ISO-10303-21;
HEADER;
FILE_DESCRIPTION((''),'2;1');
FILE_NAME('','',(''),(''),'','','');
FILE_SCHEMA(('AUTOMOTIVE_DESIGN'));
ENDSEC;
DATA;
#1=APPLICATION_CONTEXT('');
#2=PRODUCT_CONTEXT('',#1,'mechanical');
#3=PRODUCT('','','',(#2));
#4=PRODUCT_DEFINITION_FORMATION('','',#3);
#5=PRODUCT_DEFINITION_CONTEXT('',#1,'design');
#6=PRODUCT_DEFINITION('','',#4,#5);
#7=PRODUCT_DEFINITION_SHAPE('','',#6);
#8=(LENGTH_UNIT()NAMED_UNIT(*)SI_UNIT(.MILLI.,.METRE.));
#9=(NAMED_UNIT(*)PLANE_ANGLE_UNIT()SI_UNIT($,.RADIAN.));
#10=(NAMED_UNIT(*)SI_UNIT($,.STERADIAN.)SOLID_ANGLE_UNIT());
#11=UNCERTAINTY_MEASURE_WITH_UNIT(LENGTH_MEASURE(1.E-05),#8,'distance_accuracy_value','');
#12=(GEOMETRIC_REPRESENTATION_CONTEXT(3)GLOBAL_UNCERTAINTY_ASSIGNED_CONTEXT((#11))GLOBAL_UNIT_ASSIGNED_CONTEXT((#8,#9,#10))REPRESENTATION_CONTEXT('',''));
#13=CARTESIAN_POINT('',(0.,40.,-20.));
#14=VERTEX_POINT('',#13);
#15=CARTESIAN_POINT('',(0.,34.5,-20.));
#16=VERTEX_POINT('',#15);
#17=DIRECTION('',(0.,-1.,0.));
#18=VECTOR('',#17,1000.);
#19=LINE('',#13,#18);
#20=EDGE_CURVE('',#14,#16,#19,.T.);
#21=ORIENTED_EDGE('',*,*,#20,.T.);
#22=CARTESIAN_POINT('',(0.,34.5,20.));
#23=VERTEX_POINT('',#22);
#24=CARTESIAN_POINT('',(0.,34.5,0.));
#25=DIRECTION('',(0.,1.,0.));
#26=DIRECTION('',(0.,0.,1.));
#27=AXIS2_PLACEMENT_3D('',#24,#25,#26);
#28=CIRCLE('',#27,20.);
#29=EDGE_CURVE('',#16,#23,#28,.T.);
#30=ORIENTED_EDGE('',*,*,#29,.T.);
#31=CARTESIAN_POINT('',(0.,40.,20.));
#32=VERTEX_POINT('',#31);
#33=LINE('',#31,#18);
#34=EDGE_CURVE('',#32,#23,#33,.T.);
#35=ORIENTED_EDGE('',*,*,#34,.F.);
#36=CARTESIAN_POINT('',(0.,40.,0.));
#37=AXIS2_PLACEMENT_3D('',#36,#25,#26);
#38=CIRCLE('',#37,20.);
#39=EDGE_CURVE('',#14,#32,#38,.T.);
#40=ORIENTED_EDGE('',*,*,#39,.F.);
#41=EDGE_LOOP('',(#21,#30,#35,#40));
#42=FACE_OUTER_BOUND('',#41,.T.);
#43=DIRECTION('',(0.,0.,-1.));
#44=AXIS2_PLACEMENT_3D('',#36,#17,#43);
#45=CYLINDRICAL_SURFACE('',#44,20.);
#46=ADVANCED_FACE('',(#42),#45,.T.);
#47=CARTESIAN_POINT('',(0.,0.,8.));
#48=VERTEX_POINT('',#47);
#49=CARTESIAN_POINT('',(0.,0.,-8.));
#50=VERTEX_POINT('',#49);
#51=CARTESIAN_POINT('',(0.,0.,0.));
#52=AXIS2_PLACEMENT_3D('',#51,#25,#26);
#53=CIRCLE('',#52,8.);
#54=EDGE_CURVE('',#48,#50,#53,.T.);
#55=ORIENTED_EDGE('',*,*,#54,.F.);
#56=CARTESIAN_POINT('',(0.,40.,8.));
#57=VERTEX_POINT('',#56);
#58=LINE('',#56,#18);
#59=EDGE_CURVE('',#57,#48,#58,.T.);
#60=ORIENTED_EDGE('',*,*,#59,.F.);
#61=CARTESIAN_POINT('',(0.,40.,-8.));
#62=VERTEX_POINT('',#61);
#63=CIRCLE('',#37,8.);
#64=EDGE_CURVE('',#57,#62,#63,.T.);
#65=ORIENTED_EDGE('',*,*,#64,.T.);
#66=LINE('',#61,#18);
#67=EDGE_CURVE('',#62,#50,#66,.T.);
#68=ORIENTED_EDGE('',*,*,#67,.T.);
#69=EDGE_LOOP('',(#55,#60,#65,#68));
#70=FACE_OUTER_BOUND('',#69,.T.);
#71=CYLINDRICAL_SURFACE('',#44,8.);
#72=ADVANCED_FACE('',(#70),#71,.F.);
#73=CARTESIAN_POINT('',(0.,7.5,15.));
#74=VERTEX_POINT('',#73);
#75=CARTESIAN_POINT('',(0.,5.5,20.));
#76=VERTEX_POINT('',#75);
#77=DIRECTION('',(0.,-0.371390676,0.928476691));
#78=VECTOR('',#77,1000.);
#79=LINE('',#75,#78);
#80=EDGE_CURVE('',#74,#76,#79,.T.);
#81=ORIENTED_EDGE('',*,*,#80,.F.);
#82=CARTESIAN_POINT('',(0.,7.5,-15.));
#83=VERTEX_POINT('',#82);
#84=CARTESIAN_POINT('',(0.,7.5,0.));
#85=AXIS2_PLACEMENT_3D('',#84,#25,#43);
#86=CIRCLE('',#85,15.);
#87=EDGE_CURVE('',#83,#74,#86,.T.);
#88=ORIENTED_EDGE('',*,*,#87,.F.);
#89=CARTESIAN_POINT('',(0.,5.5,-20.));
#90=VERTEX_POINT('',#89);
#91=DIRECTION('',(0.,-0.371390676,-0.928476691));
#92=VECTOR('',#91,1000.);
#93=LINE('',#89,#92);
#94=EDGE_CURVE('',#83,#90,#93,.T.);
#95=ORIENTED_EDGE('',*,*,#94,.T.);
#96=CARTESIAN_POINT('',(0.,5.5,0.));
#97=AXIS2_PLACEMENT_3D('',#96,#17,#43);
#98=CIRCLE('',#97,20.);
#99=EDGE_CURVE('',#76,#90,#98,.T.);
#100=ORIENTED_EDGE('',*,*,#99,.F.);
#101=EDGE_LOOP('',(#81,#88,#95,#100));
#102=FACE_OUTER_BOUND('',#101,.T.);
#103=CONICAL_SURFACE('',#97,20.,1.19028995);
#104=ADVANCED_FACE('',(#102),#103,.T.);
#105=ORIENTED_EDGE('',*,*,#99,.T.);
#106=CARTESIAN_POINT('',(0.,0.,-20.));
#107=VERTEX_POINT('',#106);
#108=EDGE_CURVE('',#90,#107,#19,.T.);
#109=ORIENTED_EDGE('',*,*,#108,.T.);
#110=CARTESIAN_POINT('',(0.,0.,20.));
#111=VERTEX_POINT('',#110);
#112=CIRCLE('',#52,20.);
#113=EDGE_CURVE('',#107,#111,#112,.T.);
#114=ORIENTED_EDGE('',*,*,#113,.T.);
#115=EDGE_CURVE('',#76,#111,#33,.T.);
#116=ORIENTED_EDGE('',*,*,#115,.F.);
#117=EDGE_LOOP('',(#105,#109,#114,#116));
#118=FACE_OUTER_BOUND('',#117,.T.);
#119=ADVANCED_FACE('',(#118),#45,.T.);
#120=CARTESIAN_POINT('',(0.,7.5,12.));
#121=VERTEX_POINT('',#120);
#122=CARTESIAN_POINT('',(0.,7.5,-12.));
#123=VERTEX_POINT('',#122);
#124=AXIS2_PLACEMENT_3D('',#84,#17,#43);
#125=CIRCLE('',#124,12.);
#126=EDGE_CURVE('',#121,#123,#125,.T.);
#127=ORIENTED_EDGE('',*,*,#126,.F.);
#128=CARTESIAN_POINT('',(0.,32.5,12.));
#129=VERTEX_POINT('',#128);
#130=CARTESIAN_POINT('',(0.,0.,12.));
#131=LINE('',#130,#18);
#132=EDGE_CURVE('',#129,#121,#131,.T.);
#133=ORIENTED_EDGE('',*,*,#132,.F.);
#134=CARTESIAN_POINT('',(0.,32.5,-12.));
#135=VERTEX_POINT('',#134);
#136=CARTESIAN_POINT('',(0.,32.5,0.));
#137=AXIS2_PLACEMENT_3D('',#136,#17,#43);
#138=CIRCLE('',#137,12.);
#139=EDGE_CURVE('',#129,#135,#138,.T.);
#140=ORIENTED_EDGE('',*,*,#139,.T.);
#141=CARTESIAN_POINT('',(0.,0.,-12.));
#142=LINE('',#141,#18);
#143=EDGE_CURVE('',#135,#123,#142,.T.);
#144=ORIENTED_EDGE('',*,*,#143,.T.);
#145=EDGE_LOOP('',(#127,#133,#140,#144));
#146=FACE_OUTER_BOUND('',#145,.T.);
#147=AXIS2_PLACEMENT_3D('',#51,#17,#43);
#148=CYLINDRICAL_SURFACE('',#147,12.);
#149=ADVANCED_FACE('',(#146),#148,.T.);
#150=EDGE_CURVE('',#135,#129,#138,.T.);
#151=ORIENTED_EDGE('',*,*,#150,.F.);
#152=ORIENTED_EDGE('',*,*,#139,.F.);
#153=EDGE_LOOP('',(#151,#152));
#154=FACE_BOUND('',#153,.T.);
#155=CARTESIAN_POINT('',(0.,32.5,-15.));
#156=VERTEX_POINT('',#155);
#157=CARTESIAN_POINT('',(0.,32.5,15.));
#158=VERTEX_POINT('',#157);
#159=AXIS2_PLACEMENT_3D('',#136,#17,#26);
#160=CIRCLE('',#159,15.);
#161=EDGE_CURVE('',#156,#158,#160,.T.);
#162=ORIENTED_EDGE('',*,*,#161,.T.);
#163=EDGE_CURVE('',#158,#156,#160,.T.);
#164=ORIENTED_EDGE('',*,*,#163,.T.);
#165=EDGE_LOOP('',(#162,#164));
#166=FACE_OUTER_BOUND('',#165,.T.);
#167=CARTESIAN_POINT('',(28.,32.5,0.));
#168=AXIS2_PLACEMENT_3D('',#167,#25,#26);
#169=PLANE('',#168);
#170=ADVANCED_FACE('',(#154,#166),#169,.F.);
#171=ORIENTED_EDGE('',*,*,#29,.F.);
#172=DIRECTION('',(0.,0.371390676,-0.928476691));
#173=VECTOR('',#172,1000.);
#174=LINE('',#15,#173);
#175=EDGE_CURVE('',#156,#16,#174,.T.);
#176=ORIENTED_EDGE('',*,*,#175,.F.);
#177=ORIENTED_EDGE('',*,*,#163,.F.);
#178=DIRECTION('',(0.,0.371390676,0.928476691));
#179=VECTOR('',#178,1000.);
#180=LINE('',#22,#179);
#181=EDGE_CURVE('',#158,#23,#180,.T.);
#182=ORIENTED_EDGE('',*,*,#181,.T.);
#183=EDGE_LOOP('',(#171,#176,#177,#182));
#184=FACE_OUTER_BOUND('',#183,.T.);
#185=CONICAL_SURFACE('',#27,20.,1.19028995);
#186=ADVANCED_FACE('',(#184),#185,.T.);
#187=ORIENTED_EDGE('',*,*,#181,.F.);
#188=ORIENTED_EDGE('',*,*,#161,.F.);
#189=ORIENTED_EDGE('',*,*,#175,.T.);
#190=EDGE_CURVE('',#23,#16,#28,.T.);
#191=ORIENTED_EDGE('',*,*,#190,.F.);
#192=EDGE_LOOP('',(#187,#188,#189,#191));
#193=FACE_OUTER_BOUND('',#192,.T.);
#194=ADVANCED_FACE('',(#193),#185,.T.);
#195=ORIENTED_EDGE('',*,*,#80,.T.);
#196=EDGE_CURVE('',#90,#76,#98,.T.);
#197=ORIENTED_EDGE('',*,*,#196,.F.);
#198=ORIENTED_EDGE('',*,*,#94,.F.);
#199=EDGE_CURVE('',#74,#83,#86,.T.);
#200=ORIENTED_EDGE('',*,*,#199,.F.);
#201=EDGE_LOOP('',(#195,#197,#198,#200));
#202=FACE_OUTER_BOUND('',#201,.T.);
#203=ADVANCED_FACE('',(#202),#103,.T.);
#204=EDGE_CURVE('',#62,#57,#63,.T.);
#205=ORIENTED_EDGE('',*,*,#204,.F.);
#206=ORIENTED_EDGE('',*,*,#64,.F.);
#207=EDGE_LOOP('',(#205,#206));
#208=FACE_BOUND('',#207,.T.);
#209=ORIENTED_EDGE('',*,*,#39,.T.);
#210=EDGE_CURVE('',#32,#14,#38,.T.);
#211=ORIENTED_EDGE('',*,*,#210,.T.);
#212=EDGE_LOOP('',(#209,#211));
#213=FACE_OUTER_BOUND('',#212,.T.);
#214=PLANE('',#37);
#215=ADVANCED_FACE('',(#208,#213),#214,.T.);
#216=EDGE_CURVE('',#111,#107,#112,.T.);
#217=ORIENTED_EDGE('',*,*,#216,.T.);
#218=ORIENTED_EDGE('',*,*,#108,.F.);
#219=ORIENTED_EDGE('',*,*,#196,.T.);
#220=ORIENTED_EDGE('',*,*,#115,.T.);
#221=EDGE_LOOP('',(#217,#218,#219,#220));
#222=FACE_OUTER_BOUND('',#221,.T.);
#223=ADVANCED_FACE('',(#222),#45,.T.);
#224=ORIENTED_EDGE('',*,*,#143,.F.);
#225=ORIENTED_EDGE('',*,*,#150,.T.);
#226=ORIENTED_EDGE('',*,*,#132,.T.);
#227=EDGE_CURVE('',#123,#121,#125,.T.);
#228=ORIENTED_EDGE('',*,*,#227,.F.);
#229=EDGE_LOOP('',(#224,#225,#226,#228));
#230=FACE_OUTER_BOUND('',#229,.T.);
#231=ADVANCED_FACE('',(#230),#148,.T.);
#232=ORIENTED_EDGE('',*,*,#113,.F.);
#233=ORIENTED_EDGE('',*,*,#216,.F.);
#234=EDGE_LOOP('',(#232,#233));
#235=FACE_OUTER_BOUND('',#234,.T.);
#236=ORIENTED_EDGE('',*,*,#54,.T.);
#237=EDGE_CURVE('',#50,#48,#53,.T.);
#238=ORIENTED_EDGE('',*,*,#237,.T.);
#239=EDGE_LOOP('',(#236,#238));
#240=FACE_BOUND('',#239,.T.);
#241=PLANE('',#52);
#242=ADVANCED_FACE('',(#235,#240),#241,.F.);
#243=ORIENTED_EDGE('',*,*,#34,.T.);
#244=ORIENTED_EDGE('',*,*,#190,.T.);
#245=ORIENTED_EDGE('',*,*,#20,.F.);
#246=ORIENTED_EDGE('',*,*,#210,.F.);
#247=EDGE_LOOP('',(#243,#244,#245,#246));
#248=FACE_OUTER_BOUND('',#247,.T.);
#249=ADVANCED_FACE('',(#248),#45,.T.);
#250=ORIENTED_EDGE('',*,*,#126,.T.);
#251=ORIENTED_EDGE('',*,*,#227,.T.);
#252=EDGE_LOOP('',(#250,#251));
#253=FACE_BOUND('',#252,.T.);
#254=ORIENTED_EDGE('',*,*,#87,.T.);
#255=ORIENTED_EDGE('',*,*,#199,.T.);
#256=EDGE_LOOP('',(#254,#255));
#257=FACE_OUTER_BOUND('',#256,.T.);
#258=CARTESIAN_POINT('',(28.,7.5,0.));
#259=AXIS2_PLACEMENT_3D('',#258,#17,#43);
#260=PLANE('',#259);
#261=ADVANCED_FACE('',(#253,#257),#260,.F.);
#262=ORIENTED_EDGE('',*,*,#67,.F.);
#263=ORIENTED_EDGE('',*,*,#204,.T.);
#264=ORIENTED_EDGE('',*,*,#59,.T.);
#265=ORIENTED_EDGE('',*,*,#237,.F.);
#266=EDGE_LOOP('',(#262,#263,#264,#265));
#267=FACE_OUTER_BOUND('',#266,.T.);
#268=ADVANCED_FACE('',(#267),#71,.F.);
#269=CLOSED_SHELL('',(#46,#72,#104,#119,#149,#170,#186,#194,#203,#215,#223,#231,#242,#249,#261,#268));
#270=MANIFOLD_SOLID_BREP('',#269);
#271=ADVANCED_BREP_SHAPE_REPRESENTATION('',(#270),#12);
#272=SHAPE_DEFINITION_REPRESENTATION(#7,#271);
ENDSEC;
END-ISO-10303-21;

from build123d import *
from OCP.BRepFilletAPI import BRepFilletAPI_MakeChamfer

# Parameters (mm, degrees)
SKETCH1_R           = 20
SKETCH1_R_2         = 8
BOSS_EXTRUDE1_DEPTH = 40
SKETCH2_W           = 16
SKETCH2_H           = 25
CHAMFER1_SIZE       = 5
CHAMFER1_SIZE2      = 2


with BuildPart() as part:
    # Sketch1 → Boss-Extrude1 (new body)
    with BuildSketch(Plane(origin=(0, 0, 0), x_dir=(1, 0, 0), z_dir=(0, 1, 0))):
        with Locations(Location((0, 0, 0), (0, 0, 270))):
            Circle(SKETCH1_R)
        with Locations(Location((0, 0, 0), (0, 0, 270))):
            Circle(SKETCH1_R_2, mode=Mode.SUBTRACT)
    extrude(amount=BOSS_EXTRUDE1_DEPTH)

    # Sketch2 → Cut-Revolve1 (revolve, cut)
    with BuildSketch(Plane.XY, mode=Mode.PRIVATE) as cut_revolve1_sk:
        with Locations((20, 20)):
            Rectangle(SKETCH2_W, SKETCH2_H)
    revolve(cut_revolve1_sk.sketch.rotate(Axis((0, 0, 0), (0, 1, 0)), 90), axis=Axis((0, 0, 0), (0, 1, 0)), mode=Mode.SUBTRACT)

    # Chamfer1: one chamfer whose edges measure the first distance from different faces: ONE call of the kernel's chamfer builder (chamfer() names one face for all edges)
    chamfer1_edges_1 = [part.edges().sort_by_distance(p)[0] for p in [
        (0, 7.5, -20),
    ]]
    chamfer1_side_1 = [part.faces().sort_by_distance(p)[0] for p in [
        (0, 7.5, -19.434314575),
    ]]
    chamfer1_edges_2 = [part.edges().sort_by_distance(p)[0] for p in [
        (0, 32.5, -20),
    ]]
    chamfer1_side_2 = [part.faces().sort_by_distance(p)[0] for p in [
        (0, 32.5, -19.434314575),
    ]]
    chamfer1 = BRepFilletAPI_MakeChamfer(part.part.solid().wrapped)
    for e in chamfer1_edges_1:
        chamfer1.Add(CHAMFER1_SIZE, CHAMFER1_SIZE2, e.wrapped, chamfer1_side_1[0].wrapped)  # the first distance lies on this face
    for e in chamfer1_edges_2:
        chamfer1.Add(CHAMFER1_SIZE, CHAMFER1_SIZE2, e.wrapped, chamfer1_side_2[0].wrapped)  # the first distance lies on this face
    add(Compound.cast(chamfer1.Shape()), mode=Mode.REPLACE)


solid = part.part
